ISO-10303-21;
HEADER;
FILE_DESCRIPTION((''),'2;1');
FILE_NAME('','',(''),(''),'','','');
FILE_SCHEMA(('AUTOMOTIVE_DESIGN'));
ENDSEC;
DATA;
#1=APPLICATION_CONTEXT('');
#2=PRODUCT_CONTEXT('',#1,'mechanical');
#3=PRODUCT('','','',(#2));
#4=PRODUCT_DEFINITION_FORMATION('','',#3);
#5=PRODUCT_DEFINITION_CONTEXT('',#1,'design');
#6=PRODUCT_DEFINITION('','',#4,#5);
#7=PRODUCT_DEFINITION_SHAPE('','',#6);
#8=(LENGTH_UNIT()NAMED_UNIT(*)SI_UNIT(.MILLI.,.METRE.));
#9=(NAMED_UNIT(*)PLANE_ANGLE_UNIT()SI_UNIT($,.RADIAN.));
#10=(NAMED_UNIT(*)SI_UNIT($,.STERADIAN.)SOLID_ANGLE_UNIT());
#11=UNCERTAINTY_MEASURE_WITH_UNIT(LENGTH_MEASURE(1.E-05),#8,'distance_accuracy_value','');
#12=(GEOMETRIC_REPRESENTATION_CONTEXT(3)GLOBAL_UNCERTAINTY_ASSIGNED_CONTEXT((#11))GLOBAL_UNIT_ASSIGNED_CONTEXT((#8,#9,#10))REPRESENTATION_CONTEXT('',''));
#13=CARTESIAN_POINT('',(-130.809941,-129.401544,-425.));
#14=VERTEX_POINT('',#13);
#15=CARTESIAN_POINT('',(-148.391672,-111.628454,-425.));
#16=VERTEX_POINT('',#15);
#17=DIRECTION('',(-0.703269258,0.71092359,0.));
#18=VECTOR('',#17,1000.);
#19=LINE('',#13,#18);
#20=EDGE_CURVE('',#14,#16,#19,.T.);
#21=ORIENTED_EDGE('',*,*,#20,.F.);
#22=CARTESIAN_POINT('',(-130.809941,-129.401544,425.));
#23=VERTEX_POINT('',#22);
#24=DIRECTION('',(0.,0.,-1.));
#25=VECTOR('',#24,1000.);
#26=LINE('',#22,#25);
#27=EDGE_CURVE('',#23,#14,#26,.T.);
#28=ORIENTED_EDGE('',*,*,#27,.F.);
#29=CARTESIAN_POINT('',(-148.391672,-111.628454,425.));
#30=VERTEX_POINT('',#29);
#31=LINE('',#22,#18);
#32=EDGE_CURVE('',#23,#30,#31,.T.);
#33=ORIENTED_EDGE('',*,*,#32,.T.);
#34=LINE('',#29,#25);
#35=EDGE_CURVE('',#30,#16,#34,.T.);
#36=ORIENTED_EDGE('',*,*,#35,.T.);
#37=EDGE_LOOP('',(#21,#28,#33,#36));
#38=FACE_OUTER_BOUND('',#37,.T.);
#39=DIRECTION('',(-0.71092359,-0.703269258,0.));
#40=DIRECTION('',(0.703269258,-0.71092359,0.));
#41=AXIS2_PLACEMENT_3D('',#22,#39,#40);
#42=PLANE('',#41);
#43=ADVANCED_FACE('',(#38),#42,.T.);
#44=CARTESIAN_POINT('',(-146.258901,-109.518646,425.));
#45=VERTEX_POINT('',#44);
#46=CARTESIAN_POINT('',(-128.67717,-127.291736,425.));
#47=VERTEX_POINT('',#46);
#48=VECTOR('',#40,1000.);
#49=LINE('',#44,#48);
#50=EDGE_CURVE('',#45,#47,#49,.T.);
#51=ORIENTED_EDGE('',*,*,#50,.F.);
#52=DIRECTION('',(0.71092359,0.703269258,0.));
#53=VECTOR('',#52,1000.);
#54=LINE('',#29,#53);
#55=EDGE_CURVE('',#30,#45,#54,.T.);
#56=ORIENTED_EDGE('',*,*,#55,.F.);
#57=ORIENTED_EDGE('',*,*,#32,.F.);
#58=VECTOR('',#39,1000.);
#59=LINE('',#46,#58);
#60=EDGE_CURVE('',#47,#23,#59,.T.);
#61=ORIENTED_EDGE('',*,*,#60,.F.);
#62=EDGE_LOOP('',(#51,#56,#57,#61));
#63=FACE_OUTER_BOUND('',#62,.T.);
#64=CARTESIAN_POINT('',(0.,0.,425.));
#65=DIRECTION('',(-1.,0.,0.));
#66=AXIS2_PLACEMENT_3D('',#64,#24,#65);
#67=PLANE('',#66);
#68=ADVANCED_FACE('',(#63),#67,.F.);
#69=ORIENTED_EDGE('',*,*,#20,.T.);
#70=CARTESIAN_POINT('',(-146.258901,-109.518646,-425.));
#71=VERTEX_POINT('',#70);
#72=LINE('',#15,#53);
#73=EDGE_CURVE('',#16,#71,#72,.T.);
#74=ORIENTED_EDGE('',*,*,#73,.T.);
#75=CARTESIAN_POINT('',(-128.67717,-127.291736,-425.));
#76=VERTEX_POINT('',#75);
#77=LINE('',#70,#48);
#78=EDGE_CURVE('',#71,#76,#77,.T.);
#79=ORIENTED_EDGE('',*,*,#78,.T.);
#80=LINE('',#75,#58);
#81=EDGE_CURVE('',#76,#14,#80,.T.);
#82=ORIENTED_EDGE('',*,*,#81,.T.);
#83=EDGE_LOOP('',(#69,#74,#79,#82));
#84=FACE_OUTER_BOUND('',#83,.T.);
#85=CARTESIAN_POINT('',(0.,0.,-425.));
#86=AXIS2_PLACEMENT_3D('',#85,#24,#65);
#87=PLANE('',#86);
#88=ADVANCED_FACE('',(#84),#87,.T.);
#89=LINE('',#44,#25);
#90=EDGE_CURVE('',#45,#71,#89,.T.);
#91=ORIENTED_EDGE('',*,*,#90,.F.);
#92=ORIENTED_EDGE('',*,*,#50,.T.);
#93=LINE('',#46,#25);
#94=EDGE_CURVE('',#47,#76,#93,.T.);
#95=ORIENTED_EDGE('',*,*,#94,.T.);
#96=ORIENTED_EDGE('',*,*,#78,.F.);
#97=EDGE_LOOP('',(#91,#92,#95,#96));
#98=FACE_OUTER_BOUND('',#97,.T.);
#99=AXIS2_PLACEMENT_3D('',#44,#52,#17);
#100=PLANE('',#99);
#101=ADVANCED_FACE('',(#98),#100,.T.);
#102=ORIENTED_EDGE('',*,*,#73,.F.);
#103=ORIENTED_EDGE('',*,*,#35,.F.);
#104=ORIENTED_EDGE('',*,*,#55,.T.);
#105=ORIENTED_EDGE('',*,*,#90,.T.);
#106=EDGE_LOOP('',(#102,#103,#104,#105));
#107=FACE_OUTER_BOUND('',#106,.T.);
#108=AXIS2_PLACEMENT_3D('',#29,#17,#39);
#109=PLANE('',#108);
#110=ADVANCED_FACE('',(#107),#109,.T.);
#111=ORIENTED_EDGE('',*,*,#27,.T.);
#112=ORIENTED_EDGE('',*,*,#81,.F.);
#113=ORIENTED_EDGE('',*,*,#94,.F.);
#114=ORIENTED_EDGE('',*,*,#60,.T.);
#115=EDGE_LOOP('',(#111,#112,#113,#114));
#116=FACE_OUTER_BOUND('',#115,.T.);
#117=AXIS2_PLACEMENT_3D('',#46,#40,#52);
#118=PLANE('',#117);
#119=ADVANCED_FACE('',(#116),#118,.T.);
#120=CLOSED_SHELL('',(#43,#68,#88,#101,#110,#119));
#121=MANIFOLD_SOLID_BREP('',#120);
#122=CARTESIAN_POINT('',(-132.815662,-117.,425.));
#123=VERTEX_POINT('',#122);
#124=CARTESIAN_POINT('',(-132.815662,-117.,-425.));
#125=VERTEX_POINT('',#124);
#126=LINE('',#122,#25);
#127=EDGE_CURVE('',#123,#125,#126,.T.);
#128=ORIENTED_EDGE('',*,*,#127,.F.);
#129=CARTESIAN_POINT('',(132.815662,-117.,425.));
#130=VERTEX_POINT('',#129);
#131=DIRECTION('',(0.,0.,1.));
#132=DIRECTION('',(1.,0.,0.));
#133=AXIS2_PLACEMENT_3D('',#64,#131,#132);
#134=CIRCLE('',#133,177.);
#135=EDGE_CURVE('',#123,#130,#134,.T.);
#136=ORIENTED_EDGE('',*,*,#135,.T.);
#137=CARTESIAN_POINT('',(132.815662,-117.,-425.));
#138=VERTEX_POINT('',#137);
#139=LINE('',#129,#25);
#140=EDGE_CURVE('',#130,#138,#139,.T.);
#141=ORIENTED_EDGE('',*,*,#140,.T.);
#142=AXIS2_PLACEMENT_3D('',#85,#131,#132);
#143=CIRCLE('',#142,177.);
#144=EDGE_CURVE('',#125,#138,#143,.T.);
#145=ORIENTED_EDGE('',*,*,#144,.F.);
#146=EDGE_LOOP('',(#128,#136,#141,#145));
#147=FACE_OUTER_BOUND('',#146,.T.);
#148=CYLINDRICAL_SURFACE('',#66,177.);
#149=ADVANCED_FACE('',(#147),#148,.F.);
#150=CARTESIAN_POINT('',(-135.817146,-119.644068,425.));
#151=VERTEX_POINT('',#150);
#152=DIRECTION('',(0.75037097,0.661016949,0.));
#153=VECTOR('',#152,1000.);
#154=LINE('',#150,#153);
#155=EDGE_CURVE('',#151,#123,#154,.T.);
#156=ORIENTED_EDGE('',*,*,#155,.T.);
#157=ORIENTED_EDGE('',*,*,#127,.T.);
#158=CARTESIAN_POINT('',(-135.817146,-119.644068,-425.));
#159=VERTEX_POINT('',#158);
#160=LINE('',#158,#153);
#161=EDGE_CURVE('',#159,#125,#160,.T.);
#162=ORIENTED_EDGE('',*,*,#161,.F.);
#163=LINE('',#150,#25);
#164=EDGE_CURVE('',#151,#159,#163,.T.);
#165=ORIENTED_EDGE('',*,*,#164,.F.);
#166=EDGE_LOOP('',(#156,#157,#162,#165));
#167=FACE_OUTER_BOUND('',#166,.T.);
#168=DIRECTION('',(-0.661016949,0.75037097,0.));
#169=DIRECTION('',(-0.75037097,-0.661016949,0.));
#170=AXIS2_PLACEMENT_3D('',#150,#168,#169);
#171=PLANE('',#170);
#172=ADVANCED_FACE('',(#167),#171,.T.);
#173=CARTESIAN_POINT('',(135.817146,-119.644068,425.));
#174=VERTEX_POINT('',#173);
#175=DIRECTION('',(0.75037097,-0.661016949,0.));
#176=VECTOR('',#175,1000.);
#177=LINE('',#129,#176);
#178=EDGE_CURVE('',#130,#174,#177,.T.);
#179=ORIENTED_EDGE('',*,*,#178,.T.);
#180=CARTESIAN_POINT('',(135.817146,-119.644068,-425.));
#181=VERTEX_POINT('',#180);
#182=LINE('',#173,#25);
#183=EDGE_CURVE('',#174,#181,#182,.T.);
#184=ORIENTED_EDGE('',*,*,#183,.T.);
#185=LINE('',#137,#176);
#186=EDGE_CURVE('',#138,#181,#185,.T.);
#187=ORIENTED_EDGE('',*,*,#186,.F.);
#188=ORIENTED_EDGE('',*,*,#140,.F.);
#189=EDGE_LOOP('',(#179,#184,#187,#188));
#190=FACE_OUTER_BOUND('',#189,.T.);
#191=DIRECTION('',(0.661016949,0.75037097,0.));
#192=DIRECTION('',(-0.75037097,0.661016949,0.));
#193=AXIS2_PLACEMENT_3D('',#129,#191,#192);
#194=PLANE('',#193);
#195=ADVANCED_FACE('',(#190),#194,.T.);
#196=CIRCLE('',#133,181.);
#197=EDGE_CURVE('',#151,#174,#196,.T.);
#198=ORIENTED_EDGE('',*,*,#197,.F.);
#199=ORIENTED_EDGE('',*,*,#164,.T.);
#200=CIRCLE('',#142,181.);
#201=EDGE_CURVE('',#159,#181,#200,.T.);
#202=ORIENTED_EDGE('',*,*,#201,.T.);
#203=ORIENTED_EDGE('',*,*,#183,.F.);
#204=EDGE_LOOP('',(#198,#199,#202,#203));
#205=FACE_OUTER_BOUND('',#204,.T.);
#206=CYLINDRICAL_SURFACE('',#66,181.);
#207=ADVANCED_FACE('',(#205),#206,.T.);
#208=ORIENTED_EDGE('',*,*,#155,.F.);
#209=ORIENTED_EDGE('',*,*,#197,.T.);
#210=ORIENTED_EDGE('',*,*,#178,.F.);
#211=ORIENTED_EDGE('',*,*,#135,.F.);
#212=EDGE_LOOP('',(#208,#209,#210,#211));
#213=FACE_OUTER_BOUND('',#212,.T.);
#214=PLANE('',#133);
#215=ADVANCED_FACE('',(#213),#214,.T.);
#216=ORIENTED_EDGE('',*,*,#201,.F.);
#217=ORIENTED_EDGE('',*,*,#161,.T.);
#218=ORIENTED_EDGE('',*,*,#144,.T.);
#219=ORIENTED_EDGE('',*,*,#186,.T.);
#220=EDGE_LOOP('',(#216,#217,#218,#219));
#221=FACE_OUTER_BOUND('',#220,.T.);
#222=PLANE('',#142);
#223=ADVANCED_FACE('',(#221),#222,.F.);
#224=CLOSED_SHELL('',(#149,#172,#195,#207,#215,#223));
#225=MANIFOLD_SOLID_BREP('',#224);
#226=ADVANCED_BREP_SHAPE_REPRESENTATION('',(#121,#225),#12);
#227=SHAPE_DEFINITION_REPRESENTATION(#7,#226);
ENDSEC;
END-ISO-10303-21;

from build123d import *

# Parameters (mm, degrees)
EXTRUDE_1_DEPTH   = 425
EXTRUDE_1_2_DEPTH = 850


with BuildPart() as part:
    # 草图1 → Extrude 1 (new, symmetric)
    with BuildSketch(Plane.XY):
        with BuildLine():
            ThreePointArc((-132.815661727, -117), (0, -177), (132.815661727, -117))
            Line((132.815661727, -117), (135.817145608, -119.644067797))
            ThreePointArc((135.817145608, -119.644067797), (0, -181), (-135.817145608, -119.644067797))
            Line((-135.817145608, -119.644067797), (-132.815661727, -117))
        make_face()
    extrude(amount=EXTRUDE_1_DEPTH, both=True)


with BuildPart() as body_2:
    # 草图2 → Extrude 1 2 (new, through all)
    with BuildSketch(Plane(origin=(0, 0, -425), x_dir=(-1, 0, 0), z_dir=(0, 0, -1))):
        Polygon((146.258901195, -109.518645999), (128.677169739, -127.291735742), (130.809940508, -129.401543516), (148.391671964, -111.628453773), align=None)
    extrude(amount=-EXTRUDE_1_2_DEPTH)


solid = Compound([part.part, body_2.part])
